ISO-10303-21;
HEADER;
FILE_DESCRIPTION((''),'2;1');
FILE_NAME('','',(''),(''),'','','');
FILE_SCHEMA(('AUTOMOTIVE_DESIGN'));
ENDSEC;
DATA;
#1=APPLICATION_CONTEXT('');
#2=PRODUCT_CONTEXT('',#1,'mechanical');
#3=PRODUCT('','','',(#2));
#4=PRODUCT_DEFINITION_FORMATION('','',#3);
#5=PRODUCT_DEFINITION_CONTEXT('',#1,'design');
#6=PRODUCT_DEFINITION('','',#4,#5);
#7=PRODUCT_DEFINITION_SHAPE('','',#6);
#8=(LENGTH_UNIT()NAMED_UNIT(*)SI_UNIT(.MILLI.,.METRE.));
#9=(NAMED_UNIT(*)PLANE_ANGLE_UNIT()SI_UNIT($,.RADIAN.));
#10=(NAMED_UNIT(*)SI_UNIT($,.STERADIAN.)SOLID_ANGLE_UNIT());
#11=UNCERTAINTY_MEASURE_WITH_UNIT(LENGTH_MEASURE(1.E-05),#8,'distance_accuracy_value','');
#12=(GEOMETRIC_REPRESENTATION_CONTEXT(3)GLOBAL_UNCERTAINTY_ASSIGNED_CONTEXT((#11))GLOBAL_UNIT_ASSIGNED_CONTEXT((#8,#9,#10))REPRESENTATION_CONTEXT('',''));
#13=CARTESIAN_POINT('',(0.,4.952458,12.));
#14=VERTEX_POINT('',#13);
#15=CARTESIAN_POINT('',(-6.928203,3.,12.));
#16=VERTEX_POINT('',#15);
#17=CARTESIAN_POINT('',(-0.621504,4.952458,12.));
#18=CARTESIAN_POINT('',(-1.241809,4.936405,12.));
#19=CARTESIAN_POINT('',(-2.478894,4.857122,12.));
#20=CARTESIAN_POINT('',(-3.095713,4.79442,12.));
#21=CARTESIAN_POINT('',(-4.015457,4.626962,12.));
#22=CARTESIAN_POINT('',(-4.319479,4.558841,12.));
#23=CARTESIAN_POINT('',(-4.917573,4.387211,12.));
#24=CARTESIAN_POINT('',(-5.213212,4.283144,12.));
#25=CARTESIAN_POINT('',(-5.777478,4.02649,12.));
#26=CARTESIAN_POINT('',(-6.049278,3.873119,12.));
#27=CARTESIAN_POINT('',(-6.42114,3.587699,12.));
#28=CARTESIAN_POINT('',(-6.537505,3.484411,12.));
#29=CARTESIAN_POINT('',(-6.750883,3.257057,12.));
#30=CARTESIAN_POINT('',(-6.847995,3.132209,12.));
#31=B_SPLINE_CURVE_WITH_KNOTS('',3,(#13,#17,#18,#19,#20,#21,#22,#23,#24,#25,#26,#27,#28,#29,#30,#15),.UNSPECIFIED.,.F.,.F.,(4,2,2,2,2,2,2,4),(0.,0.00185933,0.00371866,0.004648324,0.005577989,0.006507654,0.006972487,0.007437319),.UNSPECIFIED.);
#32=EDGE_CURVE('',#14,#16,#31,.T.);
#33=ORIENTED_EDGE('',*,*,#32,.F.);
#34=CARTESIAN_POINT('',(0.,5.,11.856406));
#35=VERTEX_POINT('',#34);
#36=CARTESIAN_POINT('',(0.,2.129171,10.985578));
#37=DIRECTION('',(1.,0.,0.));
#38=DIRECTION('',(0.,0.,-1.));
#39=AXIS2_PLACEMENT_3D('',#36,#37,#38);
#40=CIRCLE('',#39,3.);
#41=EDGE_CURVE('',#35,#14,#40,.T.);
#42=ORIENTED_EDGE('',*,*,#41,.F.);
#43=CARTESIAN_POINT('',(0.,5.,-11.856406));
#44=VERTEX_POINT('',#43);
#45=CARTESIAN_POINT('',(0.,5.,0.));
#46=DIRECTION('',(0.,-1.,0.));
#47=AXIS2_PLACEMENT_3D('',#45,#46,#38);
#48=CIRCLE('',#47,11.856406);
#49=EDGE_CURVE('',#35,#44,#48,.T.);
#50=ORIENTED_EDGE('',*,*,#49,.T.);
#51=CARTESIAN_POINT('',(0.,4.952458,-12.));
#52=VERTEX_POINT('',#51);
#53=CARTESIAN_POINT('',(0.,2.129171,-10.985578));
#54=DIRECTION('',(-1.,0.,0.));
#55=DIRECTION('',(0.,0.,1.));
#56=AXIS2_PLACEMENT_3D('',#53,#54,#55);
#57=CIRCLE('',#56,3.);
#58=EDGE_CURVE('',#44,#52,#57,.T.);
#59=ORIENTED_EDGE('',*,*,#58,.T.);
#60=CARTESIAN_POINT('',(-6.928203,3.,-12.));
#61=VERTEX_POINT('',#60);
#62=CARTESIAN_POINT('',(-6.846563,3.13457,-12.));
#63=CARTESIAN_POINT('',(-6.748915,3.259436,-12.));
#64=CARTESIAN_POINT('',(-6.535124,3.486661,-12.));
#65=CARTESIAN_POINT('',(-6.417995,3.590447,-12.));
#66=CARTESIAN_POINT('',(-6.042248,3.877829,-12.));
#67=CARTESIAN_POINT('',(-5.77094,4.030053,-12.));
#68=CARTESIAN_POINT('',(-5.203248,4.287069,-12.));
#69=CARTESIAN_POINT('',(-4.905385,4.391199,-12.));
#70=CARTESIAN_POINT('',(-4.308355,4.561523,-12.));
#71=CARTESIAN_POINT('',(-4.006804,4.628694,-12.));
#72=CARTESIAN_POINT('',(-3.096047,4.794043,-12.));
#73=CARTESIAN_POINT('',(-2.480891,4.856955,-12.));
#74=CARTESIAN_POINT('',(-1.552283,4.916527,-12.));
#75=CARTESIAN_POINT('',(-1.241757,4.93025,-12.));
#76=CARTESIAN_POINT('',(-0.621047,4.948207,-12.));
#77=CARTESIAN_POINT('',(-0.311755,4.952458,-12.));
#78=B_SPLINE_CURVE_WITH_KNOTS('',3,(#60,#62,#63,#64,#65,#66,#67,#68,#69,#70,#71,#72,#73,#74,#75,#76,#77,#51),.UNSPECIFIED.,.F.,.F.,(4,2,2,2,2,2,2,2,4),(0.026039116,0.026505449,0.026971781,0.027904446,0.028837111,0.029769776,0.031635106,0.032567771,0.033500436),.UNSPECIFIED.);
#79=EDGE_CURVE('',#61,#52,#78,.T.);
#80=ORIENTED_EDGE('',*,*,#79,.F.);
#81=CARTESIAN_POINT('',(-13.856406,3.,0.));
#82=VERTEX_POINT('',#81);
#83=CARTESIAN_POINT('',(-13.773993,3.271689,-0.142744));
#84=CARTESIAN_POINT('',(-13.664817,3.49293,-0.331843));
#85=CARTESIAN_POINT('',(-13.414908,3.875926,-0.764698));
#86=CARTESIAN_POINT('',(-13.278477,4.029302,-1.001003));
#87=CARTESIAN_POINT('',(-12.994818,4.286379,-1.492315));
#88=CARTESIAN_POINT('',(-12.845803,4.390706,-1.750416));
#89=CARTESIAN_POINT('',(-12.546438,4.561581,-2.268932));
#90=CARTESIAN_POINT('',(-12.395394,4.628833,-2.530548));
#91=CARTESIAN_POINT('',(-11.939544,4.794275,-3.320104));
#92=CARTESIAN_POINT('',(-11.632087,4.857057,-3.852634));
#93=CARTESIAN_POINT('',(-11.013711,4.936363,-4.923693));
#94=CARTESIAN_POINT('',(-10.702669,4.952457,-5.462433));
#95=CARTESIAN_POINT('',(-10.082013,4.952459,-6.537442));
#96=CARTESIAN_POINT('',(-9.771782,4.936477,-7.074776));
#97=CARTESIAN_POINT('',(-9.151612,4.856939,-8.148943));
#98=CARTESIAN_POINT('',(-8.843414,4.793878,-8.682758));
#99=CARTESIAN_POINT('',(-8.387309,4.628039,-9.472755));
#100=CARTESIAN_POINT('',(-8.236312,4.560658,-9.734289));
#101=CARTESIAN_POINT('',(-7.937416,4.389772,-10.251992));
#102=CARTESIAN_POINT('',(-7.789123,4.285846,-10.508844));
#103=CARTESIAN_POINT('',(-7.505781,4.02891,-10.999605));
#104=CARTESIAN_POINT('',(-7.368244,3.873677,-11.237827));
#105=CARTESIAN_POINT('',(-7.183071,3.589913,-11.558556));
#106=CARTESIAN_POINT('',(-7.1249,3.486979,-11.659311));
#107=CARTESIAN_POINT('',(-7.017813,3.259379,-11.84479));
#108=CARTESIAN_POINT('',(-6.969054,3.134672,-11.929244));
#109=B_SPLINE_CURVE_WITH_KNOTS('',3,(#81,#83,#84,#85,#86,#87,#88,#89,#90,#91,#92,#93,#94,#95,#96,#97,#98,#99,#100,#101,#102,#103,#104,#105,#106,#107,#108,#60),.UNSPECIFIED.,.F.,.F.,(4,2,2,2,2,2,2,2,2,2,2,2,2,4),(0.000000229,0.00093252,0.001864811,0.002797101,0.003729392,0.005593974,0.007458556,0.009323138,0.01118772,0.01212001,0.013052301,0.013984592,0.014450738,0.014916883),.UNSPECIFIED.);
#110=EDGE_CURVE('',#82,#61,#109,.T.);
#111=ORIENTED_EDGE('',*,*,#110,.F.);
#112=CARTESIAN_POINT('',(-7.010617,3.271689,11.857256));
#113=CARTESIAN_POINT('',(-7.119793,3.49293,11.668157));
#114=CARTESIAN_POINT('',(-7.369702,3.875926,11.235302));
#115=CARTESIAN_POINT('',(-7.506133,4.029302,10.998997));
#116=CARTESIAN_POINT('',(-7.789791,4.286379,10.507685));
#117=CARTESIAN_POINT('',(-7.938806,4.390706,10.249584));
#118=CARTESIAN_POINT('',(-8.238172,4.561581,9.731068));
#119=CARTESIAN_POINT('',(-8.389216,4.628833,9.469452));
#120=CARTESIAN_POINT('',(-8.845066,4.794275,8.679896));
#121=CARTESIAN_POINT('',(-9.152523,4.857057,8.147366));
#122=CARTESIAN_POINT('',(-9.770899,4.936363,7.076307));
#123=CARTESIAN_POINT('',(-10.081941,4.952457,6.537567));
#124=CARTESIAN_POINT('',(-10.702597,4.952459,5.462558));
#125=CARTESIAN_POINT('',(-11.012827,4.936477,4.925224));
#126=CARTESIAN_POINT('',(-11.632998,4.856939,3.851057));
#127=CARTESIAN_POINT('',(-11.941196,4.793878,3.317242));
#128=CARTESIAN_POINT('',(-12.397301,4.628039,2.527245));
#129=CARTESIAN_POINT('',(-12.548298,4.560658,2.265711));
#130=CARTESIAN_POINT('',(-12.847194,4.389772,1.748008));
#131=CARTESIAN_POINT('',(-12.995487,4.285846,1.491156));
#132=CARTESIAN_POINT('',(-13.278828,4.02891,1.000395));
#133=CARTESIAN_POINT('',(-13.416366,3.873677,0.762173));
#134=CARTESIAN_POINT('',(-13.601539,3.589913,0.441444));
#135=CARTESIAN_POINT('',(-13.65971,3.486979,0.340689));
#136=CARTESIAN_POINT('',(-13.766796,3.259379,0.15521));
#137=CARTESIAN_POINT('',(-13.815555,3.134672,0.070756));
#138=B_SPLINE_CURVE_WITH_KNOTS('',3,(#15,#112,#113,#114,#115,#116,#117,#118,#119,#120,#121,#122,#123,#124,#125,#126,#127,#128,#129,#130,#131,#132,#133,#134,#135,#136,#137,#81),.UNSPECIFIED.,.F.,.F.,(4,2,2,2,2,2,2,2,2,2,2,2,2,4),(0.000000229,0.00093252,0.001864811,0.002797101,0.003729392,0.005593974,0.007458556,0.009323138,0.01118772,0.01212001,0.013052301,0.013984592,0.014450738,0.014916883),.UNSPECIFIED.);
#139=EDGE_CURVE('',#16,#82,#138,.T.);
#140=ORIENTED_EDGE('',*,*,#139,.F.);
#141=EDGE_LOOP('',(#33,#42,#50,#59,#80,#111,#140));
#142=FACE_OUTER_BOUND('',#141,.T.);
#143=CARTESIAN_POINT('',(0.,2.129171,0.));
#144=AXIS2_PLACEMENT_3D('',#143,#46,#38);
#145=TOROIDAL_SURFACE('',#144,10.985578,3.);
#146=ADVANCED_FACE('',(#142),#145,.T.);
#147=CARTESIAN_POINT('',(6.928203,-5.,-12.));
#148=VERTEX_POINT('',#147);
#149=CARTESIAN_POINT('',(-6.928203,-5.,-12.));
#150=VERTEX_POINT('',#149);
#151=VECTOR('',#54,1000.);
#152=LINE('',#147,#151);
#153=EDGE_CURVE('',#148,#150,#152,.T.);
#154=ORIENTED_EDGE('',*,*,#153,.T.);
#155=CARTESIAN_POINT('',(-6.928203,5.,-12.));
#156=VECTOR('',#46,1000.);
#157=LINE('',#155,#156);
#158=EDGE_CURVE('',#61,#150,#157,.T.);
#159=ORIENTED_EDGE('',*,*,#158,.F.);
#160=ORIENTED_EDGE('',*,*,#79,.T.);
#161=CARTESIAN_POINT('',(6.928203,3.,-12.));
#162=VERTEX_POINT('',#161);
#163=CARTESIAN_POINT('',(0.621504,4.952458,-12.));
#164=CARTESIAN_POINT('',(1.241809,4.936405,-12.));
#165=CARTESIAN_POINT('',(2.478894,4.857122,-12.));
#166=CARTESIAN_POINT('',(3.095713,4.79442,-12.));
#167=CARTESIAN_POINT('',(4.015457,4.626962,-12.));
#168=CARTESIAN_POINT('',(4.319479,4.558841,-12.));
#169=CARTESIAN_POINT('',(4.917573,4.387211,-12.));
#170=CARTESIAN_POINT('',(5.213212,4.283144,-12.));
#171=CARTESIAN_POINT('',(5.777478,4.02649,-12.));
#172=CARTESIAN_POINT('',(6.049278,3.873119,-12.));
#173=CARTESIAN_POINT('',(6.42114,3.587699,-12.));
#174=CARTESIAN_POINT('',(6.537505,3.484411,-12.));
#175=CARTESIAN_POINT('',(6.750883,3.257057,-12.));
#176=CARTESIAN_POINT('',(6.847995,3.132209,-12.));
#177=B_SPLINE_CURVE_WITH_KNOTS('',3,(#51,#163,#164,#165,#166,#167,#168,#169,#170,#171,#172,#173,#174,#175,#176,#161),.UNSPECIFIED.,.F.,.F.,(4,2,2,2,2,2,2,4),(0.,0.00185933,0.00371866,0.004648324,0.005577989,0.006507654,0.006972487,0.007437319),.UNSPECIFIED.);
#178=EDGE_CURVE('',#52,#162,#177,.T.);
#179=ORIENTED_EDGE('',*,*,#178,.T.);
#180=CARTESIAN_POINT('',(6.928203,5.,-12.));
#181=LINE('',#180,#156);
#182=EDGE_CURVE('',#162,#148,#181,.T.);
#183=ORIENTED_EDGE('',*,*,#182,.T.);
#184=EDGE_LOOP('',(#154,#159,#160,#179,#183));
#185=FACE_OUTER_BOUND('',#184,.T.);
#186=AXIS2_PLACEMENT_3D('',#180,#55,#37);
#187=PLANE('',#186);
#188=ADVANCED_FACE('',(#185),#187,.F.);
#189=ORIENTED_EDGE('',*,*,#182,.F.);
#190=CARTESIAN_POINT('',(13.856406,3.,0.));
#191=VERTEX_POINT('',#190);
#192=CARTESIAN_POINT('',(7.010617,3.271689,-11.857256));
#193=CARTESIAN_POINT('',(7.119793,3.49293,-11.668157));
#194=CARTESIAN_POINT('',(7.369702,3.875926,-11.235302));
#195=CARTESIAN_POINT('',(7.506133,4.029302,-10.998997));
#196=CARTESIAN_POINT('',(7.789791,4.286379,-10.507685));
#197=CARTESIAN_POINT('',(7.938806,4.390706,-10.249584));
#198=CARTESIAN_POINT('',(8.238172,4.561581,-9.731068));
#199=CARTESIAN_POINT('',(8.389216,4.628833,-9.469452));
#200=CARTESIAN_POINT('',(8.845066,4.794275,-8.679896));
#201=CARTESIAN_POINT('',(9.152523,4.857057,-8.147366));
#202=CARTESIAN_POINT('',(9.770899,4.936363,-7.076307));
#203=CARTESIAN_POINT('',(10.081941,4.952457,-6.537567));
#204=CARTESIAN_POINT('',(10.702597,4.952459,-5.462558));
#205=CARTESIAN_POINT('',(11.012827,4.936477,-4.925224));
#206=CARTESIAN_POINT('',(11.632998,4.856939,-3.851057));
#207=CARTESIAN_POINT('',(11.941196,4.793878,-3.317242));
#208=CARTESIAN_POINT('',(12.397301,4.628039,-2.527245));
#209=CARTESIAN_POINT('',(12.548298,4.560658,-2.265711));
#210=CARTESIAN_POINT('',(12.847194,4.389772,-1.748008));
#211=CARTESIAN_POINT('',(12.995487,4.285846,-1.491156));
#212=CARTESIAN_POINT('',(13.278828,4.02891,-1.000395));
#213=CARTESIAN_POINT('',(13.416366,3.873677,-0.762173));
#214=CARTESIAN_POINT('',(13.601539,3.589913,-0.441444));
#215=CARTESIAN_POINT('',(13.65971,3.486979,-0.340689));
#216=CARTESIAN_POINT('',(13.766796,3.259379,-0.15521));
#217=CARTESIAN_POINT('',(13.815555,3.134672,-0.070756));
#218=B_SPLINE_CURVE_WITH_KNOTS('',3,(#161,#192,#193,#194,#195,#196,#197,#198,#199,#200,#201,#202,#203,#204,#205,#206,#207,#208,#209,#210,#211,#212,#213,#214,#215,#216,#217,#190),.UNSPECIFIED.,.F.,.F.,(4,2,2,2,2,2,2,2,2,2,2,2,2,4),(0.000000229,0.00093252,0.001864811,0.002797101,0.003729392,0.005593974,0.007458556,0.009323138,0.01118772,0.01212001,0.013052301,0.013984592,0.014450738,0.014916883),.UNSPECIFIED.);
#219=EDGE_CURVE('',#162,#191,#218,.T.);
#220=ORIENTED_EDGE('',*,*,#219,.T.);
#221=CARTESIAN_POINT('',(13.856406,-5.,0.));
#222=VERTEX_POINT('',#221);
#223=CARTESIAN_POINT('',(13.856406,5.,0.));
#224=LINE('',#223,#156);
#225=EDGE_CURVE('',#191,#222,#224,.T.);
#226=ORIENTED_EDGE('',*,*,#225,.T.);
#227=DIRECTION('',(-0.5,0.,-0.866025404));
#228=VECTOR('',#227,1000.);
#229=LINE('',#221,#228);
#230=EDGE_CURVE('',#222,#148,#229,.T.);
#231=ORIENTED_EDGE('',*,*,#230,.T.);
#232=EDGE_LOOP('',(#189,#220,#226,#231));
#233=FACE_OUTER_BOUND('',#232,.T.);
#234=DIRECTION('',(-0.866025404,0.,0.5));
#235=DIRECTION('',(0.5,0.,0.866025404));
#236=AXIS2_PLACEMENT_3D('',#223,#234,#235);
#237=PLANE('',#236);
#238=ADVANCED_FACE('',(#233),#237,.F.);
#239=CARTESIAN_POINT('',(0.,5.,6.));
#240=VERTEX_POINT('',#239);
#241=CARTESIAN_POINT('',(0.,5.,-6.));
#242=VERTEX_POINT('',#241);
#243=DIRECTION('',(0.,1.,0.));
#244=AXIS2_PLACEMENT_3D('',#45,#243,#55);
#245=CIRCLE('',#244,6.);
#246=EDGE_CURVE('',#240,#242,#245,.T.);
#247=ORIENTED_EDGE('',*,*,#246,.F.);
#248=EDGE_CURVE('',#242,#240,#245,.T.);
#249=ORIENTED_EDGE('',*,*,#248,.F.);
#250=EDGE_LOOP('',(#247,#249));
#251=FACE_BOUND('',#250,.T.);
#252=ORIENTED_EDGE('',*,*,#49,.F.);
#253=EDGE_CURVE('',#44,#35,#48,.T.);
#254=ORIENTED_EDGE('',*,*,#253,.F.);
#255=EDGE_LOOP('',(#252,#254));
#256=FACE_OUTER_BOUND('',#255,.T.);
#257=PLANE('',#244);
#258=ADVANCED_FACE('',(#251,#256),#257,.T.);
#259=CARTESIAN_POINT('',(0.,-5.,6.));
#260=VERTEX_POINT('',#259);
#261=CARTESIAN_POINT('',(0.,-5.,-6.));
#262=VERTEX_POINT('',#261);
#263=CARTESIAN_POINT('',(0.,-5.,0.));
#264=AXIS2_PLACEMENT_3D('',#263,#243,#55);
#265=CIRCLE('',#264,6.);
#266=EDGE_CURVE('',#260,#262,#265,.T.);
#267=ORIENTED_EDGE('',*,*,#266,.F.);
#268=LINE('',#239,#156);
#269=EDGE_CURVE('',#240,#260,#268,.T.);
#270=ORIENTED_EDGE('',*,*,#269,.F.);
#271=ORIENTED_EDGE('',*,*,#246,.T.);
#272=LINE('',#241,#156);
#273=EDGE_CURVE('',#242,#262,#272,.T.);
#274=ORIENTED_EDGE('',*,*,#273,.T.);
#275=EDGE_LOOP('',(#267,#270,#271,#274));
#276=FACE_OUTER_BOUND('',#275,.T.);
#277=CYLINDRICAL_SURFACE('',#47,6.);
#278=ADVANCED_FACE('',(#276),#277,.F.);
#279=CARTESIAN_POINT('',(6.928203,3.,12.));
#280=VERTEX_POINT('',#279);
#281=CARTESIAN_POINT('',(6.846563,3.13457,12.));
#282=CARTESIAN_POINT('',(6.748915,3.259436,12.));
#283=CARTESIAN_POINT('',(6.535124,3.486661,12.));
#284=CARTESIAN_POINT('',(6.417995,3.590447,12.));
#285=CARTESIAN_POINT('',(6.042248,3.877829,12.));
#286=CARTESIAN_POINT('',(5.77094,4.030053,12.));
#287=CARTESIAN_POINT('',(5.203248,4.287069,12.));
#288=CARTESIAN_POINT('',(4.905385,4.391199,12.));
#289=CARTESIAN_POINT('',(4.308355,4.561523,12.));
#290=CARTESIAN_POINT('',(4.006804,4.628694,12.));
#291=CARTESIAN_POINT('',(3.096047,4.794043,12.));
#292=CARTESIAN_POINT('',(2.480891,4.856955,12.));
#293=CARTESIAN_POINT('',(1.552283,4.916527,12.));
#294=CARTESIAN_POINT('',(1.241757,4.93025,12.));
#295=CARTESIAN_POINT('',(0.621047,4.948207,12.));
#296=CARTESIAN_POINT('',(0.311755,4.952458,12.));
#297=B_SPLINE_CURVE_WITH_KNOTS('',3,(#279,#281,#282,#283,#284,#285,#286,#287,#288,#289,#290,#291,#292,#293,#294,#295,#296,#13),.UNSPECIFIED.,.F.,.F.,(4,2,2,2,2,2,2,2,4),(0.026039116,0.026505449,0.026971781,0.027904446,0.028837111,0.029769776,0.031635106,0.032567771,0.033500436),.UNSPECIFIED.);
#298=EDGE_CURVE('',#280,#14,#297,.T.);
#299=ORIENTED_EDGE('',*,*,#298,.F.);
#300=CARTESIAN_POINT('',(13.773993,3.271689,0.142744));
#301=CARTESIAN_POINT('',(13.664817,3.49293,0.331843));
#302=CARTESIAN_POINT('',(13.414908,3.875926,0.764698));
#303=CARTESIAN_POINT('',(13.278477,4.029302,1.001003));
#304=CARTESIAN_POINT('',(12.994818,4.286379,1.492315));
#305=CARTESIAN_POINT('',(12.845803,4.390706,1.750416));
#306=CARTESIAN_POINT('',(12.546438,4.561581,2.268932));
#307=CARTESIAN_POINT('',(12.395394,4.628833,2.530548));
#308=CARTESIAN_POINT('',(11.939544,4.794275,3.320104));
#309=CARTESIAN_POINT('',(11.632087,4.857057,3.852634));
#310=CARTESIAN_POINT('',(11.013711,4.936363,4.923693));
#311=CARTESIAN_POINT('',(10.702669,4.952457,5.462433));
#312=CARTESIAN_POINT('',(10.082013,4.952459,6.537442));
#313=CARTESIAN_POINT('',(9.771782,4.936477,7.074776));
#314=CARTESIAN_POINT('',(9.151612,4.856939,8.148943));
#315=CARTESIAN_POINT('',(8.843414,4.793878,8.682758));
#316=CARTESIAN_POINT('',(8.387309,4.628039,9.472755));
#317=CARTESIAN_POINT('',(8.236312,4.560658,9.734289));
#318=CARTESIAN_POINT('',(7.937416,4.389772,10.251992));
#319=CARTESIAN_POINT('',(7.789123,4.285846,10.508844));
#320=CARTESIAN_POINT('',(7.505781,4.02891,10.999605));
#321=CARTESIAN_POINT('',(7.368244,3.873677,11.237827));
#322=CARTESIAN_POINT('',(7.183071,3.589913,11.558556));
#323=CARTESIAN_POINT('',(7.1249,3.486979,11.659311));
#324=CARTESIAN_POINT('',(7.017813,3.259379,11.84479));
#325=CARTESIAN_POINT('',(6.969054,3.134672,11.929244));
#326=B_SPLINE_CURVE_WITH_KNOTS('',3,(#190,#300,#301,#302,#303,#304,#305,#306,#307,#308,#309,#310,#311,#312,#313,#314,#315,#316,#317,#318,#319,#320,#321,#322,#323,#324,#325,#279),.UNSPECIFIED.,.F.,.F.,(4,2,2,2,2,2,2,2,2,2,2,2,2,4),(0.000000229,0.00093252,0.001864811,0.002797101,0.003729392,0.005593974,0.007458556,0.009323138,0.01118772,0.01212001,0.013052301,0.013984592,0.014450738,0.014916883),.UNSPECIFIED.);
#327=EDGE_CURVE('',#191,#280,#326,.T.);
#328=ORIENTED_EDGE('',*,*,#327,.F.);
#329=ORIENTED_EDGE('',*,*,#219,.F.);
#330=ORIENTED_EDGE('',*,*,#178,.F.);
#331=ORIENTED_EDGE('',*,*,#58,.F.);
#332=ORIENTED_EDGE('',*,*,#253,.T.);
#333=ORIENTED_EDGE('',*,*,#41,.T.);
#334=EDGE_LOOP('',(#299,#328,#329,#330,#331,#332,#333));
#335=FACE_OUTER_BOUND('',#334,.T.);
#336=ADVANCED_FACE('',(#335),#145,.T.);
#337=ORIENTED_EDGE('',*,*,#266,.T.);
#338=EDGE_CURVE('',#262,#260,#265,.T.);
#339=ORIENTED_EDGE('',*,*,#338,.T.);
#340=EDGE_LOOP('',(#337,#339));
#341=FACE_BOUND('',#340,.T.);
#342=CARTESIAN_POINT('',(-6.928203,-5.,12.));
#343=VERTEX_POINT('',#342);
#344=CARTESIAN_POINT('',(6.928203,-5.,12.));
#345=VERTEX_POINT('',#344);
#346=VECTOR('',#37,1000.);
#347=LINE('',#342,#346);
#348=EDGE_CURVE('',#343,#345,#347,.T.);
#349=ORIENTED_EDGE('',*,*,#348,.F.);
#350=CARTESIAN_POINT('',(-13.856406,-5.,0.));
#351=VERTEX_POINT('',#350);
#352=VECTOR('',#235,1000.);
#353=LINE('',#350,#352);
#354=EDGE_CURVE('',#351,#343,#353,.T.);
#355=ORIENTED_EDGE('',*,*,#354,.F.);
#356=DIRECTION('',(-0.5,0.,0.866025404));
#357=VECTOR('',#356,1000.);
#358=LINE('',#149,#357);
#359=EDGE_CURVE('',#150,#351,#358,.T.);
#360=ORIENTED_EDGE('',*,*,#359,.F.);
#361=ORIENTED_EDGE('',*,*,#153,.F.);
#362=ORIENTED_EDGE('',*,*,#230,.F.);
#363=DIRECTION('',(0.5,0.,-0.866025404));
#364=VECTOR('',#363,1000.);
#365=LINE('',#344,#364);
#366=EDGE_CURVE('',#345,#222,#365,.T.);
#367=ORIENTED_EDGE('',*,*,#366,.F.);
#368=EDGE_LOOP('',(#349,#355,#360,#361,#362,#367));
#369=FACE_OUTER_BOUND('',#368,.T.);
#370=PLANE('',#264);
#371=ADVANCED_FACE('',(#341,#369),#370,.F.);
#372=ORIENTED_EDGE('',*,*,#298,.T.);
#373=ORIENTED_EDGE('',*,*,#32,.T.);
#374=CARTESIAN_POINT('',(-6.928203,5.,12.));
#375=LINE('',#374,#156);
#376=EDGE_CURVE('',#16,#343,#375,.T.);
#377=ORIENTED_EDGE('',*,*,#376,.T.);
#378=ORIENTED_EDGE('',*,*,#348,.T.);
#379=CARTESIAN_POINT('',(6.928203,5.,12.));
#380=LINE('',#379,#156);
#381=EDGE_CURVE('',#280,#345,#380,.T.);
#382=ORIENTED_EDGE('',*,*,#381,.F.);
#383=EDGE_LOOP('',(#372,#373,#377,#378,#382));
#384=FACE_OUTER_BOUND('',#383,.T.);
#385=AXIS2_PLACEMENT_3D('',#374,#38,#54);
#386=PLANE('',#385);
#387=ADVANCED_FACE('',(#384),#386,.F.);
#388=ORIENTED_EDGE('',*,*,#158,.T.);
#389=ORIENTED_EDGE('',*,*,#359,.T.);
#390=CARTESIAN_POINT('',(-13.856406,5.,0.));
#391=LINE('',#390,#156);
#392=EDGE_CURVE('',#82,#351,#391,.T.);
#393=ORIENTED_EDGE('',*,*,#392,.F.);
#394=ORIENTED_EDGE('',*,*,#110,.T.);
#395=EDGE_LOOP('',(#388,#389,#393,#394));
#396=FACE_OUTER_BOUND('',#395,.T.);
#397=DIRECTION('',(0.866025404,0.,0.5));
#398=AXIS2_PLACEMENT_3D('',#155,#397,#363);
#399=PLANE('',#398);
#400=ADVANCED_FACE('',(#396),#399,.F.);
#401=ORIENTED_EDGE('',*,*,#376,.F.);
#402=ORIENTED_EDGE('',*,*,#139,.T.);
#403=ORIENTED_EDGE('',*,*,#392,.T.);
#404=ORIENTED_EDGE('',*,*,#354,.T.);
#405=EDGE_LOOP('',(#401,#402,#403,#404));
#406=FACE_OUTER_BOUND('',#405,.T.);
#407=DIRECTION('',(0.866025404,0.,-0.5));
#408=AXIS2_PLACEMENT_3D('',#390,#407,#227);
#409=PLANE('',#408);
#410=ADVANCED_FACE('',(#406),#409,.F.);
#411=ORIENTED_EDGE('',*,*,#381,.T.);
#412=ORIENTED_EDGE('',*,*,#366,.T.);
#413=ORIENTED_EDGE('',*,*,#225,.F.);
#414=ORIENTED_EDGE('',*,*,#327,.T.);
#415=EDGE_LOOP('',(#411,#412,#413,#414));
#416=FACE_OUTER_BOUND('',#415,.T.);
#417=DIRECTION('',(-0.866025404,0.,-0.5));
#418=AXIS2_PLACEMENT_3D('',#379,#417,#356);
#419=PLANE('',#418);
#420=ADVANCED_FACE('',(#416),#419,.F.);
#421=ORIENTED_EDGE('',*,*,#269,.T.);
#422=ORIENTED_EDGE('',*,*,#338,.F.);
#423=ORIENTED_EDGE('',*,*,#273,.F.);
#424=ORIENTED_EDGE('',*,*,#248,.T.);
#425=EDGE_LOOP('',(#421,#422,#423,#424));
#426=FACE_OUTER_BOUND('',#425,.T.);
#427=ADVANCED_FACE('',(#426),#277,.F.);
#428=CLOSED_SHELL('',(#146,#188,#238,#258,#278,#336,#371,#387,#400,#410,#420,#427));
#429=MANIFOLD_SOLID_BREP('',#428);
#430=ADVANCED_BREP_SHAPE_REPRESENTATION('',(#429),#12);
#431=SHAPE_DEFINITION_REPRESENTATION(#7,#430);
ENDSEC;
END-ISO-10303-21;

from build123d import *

# Parameters (mm, degrees)
HEX_PROFILE_SKETCH_R = 6
HEX_NUT_BODY_DEPTH   = 5


with BuildPart() as part:
    # Hex Profile Sketch → Hex Nut Body (new, symmetric)
    with BuildSketch(Plane(origin=(0, 0, 0), x_dir=(1, 0, 0), z_dir=(0, 1, 0))):
        Polygon((13.856406461, 0), (6.92820323, 12), (-6.92820323, 12), (-13.856406461, 0), (-6.92820323, -12), (6.92820323, -12), align=None)
        with Locations(Location((0, 0, 0), (0, 0, 270))):
            Circle(HEX_PROFILE_SKETCH_R, mode=Mode.SUBTRACT)
    extrude(amount=HEX_NUT_BODY_DEPTH, both=True)

    # Corner Chamfer Profile Sketch → Hex Corner Chamfer (revolve, cut)
    with BuildSketch(Plane.XY, mode=Mode.PRIVATE) as hex_corner_chamfer_sk:
        with BuildLine():
            Line((11.856406461, 5), (13.856406461, 5))
            Line((13.856406461, 5), (13.856406461, 3))
            ThreePointArc((13.856406461, 3), (13.106898111, 4.25049165), (11.856406461, 5))
        make_face()
    revolve(hex_corner_chamfer_sk.sketch.rotate(Axis((0, -7.51909737, 0), (0, 1, 0)), 90), axis=Axis((0, -7.51909737, 0), (0, 1, 0)), mode=Mode.SUBTRACT)


solid = part.part
